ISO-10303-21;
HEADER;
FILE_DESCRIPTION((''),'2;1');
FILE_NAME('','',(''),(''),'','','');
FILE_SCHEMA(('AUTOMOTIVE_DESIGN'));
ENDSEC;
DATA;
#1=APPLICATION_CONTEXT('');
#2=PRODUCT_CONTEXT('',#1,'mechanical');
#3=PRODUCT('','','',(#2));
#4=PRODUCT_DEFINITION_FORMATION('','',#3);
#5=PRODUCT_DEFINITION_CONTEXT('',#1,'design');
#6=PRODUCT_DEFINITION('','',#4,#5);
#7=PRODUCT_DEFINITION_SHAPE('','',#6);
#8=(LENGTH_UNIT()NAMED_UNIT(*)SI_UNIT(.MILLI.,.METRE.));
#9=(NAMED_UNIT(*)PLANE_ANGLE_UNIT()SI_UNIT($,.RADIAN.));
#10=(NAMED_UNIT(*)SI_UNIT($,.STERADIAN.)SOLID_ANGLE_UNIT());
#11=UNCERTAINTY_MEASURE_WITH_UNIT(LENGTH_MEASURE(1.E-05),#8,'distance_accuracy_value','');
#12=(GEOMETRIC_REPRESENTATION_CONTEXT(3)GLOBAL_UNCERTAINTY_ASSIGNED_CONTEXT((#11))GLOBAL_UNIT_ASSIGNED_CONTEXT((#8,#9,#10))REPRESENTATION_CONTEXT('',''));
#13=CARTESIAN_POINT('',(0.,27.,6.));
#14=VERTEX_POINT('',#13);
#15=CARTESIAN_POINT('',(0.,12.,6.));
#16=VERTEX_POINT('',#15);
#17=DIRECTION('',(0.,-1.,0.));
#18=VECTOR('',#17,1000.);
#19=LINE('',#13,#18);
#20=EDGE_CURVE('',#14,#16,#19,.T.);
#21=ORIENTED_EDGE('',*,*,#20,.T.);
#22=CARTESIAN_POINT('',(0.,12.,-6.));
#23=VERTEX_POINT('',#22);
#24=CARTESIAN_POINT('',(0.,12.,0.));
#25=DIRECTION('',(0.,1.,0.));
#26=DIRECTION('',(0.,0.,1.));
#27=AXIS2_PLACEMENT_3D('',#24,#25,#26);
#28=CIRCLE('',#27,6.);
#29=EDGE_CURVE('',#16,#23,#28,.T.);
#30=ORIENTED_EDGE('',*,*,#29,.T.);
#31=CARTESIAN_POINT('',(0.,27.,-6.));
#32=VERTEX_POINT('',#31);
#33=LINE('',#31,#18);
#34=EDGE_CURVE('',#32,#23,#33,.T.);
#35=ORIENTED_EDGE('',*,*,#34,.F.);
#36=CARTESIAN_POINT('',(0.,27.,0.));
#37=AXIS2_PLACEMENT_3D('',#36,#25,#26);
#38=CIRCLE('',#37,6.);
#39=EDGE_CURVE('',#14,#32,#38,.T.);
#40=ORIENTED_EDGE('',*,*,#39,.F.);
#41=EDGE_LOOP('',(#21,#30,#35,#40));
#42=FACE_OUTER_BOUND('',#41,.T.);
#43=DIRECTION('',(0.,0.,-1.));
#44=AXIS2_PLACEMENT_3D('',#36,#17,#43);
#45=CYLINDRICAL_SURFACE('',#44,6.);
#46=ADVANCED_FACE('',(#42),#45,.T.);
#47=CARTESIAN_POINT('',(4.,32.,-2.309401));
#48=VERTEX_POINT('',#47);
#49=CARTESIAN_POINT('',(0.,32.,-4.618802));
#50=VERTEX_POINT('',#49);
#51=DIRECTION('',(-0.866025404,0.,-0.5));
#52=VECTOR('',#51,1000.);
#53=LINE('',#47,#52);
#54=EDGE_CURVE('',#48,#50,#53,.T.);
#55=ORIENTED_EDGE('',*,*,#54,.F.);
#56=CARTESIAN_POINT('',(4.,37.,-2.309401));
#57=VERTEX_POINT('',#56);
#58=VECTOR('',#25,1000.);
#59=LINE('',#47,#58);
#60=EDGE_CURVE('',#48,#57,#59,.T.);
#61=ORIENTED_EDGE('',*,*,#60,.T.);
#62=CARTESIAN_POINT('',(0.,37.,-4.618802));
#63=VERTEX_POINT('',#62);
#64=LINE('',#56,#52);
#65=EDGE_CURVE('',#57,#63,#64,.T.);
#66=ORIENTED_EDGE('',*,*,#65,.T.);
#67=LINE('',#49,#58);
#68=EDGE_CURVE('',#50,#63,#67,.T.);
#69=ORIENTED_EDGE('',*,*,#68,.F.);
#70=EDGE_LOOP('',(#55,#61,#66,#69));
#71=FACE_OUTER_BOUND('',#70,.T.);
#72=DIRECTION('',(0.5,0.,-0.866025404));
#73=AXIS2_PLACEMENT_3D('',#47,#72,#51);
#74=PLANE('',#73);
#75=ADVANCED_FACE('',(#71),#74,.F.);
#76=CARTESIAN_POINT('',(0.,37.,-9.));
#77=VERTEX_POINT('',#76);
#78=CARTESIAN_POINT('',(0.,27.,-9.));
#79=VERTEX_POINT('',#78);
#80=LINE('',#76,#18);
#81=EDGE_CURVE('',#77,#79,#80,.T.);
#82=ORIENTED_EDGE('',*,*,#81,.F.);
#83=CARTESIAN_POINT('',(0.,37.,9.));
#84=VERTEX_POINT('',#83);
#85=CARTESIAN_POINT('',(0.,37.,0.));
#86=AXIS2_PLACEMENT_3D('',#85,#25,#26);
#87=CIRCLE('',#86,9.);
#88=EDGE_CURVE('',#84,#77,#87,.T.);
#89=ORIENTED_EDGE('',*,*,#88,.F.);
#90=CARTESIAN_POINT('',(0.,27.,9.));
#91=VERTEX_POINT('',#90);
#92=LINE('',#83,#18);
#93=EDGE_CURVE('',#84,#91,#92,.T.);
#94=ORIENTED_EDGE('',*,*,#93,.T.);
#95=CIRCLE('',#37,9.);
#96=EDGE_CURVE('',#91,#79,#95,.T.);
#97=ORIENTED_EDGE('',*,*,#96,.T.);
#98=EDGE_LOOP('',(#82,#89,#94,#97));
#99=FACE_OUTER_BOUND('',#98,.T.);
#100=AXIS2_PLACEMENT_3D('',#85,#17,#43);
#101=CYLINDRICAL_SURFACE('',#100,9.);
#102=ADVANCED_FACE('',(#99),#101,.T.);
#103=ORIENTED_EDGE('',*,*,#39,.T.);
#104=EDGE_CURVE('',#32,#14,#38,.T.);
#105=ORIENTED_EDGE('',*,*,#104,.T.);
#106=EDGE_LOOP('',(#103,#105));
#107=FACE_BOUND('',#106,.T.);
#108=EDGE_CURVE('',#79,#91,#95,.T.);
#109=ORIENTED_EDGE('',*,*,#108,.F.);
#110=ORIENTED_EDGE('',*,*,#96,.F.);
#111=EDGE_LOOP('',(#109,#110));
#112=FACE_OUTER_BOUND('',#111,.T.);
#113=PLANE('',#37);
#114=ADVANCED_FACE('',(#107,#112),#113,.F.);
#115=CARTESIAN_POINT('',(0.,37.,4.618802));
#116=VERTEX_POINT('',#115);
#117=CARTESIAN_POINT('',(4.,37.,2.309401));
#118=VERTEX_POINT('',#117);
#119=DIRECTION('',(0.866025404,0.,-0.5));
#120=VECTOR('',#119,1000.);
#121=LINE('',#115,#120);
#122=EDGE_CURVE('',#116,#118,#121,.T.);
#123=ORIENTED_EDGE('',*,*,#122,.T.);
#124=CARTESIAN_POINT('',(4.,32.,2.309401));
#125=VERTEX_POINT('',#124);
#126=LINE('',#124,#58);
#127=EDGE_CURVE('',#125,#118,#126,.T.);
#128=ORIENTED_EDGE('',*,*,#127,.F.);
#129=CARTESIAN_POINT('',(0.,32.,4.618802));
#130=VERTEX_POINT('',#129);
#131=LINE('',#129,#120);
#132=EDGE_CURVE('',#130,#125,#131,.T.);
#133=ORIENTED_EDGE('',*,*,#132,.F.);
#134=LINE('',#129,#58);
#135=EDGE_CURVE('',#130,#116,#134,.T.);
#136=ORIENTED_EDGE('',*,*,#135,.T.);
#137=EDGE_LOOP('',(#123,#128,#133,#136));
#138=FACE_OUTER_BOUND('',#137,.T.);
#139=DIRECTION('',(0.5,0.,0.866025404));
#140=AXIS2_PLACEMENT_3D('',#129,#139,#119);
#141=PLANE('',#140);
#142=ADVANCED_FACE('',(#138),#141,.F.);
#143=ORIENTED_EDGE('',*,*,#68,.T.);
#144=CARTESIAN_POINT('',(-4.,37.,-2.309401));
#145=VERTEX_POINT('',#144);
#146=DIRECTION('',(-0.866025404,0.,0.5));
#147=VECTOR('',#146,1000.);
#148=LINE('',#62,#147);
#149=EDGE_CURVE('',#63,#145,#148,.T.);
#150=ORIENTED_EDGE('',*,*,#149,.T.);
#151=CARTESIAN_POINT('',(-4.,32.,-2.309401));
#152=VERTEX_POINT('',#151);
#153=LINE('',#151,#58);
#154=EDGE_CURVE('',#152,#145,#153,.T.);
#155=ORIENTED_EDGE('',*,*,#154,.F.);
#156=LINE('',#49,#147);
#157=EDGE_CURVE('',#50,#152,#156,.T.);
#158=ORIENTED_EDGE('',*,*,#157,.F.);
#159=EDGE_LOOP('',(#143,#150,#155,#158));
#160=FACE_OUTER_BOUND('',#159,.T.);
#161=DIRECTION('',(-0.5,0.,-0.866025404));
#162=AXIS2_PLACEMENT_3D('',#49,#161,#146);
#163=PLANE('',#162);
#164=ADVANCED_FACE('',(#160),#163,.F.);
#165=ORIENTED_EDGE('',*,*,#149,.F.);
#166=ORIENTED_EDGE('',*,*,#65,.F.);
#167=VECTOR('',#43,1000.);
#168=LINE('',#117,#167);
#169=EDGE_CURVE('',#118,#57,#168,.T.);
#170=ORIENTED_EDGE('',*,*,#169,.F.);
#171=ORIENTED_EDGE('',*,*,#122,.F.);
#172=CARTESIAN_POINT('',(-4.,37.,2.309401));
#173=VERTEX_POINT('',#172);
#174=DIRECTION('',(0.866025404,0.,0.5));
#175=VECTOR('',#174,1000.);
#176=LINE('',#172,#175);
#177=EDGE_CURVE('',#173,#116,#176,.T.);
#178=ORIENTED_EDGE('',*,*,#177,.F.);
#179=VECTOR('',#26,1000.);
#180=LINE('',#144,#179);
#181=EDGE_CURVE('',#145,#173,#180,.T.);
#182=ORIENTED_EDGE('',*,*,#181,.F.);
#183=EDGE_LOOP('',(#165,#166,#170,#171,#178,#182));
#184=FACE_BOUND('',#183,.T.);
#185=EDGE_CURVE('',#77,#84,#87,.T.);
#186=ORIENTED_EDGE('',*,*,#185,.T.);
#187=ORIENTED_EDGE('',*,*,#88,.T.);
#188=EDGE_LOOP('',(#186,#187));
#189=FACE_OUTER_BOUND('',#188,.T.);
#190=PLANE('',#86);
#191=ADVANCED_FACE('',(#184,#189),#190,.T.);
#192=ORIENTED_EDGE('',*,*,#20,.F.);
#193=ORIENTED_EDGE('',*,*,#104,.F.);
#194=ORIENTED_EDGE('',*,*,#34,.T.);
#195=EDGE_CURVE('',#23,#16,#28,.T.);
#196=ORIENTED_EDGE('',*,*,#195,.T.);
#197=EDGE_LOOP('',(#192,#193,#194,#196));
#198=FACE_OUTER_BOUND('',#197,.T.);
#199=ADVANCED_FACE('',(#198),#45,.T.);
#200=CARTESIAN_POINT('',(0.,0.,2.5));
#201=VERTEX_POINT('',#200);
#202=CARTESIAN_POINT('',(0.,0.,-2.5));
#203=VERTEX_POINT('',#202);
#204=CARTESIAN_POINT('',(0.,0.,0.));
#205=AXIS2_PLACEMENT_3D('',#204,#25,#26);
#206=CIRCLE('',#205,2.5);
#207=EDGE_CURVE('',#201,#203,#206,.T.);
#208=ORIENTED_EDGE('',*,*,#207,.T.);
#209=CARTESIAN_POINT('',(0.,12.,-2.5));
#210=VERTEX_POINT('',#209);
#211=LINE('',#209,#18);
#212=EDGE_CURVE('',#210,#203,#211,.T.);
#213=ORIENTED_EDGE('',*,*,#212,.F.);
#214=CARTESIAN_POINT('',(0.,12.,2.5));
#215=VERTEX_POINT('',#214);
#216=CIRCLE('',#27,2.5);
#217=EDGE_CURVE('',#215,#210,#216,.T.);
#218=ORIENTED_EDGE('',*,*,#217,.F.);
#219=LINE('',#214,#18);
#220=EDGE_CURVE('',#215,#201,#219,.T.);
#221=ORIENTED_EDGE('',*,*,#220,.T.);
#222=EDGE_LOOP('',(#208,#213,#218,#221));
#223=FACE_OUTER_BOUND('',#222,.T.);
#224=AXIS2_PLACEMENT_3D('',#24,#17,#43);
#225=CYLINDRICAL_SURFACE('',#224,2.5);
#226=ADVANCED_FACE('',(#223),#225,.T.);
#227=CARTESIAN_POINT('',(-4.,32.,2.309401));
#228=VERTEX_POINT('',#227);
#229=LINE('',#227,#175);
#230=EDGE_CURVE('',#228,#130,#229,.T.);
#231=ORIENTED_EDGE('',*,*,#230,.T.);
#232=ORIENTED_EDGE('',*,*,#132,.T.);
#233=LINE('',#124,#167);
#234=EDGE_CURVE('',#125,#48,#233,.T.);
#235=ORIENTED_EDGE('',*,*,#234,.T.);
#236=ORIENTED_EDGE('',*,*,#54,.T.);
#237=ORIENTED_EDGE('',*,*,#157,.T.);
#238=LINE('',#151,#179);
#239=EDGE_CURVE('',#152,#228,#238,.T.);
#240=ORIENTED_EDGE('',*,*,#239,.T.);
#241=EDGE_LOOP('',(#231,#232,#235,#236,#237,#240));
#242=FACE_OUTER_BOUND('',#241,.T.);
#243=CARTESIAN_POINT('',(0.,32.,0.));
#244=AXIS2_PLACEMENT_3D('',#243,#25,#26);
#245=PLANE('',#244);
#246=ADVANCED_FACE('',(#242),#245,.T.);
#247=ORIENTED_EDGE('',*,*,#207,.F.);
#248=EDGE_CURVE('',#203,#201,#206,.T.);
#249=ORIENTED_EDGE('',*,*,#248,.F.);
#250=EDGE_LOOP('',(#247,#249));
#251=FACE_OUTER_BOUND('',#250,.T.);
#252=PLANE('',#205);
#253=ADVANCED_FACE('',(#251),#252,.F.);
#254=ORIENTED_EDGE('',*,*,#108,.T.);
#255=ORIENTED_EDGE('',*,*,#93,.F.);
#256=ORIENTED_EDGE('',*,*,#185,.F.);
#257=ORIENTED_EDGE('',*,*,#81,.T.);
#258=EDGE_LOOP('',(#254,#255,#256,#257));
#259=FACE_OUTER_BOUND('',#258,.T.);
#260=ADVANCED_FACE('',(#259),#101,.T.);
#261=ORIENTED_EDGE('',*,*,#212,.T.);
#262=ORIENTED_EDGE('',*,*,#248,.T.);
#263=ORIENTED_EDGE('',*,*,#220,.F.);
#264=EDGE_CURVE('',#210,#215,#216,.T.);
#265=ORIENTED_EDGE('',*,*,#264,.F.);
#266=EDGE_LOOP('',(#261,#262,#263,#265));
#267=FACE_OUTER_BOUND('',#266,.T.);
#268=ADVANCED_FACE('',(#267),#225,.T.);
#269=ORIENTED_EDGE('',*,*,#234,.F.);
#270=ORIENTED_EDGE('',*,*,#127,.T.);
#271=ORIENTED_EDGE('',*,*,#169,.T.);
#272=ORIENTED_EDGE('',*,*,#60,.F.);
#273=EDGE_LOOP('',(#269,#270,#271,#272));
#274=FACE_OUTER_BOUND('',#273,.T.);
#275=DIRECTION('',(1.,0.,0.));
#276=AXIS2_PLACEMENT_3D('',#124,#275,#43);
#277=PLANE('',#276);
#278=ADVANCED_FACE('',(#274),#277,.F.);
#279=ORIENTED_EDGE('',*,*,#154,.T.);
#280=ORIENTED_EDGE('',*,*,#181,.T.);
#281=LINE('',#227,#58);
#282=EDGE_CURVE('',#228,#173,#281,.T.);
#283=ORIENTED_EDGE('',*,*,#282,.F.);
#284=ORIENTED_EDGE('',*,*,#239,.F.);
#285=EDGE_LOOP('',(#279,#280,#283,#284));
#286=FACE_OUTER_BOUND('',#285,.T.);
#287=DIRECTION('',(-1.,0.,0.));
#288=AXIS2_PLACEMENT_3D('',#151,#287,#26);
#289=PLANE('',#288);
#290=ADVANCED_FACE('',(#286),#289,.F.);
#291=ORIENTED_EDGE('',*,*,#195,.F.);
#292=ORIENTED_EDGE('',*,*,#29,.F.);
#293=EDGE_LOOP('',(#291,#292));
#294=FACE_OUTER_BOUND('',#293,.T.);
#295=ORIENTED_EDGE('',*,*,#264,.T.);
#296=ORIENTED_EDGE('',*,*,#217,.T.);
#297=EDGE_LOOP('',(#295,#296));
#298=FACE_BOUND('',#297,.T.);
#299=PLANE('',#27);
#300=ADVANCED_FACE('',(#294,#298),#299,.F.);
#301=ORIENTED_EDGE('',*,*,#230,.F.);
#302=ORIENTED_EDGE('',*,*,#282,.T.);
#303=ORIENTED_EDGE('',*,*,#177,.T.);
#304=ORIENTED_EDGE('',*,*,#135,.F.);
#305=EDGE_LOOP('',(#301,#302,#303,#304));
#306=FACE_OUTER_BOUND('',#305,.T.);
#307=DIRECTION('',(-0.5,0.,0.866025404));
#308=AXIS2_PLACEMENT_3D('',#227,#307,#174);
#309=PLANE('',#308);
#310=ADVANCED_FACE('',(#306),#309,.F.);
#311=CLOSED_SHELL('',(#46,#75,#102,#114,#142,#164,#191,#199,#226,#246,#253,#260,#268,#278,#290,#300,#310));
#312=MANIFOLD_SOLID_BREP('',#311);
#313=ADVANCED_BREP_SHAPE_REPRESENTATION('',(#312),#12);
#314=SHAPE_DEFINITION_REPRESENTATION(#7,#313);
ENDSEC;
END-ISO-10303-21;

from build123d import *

# Parameters (mm, degrees)
SKETCH1_R           = 2.5
BOSS_EXTRUDE1_DEPTH = 12
SKETCH2_R           = 6
BOSS_EXTRUDE2_DEPTH = 15
SKETCH3_R           = 9
BOSS_EXTRUDE3_DEPTH = 10
CUT_EXTRUDE1_DEPTH  = 5


with BuildPart() as part:
    # Sketch1 → Boss-Extrude1 (new body)
    with BuildSketch(Plane(origin=(0, 0, 0), x_dir=(1, 0, 0), z_dir=(0, 1, 0))):
        with Locations(Location((0, 0, 0), (0, 0, 270))):
            Circle(SKETCH1_R)
    extrude(amount=BOSS_EXTRUDE1_DEPTH)

    # Sketch2 → Boss-Extrude2 (add)
    with BuildSketch(Plane(origin=(0, 12, 0), x_dir=(1, 0, 0), z_dir=(0, 1, 0))):
        with Locations(Location((0, 0, 0), (0, 0, 270))):
            Circle(SKETCH2_R)
    extrude(amount=BOSS_EXTRUDE2_DEPTH)

    # Sketch3 → Boss-Extrude3 (add)
    with BuildSketch(Plane(origin=(0, 27, 0), x_dir=(1, 0, 0), z_dir=(0, 1, 0))):
        with Locations(Location((0, 0, 0), (0, 0, 270))):
            Circle(SKETCH3_R)
    extrude(amount=BOSS_EXTRUDE3_DEPTH)

    # Sketch4 → Cut-Extrude1 (cut)
    with BuildSketch(Plane(origin=(0, 37, 0), x_dir=(1, 0, 0), z_dir=(0, 1, 0))):
        Polygon((0, 4.618802154), (-4, 2.309401077), (-4, -2.309401077), (0, -4.618802154), (4, -2.309401077), (4, 2.309401077), align=None)
    extrude(amount=-CUT_EXTRUDE1_DEPTH, mode=Mode.SUBTRACT)


solid = part.part
